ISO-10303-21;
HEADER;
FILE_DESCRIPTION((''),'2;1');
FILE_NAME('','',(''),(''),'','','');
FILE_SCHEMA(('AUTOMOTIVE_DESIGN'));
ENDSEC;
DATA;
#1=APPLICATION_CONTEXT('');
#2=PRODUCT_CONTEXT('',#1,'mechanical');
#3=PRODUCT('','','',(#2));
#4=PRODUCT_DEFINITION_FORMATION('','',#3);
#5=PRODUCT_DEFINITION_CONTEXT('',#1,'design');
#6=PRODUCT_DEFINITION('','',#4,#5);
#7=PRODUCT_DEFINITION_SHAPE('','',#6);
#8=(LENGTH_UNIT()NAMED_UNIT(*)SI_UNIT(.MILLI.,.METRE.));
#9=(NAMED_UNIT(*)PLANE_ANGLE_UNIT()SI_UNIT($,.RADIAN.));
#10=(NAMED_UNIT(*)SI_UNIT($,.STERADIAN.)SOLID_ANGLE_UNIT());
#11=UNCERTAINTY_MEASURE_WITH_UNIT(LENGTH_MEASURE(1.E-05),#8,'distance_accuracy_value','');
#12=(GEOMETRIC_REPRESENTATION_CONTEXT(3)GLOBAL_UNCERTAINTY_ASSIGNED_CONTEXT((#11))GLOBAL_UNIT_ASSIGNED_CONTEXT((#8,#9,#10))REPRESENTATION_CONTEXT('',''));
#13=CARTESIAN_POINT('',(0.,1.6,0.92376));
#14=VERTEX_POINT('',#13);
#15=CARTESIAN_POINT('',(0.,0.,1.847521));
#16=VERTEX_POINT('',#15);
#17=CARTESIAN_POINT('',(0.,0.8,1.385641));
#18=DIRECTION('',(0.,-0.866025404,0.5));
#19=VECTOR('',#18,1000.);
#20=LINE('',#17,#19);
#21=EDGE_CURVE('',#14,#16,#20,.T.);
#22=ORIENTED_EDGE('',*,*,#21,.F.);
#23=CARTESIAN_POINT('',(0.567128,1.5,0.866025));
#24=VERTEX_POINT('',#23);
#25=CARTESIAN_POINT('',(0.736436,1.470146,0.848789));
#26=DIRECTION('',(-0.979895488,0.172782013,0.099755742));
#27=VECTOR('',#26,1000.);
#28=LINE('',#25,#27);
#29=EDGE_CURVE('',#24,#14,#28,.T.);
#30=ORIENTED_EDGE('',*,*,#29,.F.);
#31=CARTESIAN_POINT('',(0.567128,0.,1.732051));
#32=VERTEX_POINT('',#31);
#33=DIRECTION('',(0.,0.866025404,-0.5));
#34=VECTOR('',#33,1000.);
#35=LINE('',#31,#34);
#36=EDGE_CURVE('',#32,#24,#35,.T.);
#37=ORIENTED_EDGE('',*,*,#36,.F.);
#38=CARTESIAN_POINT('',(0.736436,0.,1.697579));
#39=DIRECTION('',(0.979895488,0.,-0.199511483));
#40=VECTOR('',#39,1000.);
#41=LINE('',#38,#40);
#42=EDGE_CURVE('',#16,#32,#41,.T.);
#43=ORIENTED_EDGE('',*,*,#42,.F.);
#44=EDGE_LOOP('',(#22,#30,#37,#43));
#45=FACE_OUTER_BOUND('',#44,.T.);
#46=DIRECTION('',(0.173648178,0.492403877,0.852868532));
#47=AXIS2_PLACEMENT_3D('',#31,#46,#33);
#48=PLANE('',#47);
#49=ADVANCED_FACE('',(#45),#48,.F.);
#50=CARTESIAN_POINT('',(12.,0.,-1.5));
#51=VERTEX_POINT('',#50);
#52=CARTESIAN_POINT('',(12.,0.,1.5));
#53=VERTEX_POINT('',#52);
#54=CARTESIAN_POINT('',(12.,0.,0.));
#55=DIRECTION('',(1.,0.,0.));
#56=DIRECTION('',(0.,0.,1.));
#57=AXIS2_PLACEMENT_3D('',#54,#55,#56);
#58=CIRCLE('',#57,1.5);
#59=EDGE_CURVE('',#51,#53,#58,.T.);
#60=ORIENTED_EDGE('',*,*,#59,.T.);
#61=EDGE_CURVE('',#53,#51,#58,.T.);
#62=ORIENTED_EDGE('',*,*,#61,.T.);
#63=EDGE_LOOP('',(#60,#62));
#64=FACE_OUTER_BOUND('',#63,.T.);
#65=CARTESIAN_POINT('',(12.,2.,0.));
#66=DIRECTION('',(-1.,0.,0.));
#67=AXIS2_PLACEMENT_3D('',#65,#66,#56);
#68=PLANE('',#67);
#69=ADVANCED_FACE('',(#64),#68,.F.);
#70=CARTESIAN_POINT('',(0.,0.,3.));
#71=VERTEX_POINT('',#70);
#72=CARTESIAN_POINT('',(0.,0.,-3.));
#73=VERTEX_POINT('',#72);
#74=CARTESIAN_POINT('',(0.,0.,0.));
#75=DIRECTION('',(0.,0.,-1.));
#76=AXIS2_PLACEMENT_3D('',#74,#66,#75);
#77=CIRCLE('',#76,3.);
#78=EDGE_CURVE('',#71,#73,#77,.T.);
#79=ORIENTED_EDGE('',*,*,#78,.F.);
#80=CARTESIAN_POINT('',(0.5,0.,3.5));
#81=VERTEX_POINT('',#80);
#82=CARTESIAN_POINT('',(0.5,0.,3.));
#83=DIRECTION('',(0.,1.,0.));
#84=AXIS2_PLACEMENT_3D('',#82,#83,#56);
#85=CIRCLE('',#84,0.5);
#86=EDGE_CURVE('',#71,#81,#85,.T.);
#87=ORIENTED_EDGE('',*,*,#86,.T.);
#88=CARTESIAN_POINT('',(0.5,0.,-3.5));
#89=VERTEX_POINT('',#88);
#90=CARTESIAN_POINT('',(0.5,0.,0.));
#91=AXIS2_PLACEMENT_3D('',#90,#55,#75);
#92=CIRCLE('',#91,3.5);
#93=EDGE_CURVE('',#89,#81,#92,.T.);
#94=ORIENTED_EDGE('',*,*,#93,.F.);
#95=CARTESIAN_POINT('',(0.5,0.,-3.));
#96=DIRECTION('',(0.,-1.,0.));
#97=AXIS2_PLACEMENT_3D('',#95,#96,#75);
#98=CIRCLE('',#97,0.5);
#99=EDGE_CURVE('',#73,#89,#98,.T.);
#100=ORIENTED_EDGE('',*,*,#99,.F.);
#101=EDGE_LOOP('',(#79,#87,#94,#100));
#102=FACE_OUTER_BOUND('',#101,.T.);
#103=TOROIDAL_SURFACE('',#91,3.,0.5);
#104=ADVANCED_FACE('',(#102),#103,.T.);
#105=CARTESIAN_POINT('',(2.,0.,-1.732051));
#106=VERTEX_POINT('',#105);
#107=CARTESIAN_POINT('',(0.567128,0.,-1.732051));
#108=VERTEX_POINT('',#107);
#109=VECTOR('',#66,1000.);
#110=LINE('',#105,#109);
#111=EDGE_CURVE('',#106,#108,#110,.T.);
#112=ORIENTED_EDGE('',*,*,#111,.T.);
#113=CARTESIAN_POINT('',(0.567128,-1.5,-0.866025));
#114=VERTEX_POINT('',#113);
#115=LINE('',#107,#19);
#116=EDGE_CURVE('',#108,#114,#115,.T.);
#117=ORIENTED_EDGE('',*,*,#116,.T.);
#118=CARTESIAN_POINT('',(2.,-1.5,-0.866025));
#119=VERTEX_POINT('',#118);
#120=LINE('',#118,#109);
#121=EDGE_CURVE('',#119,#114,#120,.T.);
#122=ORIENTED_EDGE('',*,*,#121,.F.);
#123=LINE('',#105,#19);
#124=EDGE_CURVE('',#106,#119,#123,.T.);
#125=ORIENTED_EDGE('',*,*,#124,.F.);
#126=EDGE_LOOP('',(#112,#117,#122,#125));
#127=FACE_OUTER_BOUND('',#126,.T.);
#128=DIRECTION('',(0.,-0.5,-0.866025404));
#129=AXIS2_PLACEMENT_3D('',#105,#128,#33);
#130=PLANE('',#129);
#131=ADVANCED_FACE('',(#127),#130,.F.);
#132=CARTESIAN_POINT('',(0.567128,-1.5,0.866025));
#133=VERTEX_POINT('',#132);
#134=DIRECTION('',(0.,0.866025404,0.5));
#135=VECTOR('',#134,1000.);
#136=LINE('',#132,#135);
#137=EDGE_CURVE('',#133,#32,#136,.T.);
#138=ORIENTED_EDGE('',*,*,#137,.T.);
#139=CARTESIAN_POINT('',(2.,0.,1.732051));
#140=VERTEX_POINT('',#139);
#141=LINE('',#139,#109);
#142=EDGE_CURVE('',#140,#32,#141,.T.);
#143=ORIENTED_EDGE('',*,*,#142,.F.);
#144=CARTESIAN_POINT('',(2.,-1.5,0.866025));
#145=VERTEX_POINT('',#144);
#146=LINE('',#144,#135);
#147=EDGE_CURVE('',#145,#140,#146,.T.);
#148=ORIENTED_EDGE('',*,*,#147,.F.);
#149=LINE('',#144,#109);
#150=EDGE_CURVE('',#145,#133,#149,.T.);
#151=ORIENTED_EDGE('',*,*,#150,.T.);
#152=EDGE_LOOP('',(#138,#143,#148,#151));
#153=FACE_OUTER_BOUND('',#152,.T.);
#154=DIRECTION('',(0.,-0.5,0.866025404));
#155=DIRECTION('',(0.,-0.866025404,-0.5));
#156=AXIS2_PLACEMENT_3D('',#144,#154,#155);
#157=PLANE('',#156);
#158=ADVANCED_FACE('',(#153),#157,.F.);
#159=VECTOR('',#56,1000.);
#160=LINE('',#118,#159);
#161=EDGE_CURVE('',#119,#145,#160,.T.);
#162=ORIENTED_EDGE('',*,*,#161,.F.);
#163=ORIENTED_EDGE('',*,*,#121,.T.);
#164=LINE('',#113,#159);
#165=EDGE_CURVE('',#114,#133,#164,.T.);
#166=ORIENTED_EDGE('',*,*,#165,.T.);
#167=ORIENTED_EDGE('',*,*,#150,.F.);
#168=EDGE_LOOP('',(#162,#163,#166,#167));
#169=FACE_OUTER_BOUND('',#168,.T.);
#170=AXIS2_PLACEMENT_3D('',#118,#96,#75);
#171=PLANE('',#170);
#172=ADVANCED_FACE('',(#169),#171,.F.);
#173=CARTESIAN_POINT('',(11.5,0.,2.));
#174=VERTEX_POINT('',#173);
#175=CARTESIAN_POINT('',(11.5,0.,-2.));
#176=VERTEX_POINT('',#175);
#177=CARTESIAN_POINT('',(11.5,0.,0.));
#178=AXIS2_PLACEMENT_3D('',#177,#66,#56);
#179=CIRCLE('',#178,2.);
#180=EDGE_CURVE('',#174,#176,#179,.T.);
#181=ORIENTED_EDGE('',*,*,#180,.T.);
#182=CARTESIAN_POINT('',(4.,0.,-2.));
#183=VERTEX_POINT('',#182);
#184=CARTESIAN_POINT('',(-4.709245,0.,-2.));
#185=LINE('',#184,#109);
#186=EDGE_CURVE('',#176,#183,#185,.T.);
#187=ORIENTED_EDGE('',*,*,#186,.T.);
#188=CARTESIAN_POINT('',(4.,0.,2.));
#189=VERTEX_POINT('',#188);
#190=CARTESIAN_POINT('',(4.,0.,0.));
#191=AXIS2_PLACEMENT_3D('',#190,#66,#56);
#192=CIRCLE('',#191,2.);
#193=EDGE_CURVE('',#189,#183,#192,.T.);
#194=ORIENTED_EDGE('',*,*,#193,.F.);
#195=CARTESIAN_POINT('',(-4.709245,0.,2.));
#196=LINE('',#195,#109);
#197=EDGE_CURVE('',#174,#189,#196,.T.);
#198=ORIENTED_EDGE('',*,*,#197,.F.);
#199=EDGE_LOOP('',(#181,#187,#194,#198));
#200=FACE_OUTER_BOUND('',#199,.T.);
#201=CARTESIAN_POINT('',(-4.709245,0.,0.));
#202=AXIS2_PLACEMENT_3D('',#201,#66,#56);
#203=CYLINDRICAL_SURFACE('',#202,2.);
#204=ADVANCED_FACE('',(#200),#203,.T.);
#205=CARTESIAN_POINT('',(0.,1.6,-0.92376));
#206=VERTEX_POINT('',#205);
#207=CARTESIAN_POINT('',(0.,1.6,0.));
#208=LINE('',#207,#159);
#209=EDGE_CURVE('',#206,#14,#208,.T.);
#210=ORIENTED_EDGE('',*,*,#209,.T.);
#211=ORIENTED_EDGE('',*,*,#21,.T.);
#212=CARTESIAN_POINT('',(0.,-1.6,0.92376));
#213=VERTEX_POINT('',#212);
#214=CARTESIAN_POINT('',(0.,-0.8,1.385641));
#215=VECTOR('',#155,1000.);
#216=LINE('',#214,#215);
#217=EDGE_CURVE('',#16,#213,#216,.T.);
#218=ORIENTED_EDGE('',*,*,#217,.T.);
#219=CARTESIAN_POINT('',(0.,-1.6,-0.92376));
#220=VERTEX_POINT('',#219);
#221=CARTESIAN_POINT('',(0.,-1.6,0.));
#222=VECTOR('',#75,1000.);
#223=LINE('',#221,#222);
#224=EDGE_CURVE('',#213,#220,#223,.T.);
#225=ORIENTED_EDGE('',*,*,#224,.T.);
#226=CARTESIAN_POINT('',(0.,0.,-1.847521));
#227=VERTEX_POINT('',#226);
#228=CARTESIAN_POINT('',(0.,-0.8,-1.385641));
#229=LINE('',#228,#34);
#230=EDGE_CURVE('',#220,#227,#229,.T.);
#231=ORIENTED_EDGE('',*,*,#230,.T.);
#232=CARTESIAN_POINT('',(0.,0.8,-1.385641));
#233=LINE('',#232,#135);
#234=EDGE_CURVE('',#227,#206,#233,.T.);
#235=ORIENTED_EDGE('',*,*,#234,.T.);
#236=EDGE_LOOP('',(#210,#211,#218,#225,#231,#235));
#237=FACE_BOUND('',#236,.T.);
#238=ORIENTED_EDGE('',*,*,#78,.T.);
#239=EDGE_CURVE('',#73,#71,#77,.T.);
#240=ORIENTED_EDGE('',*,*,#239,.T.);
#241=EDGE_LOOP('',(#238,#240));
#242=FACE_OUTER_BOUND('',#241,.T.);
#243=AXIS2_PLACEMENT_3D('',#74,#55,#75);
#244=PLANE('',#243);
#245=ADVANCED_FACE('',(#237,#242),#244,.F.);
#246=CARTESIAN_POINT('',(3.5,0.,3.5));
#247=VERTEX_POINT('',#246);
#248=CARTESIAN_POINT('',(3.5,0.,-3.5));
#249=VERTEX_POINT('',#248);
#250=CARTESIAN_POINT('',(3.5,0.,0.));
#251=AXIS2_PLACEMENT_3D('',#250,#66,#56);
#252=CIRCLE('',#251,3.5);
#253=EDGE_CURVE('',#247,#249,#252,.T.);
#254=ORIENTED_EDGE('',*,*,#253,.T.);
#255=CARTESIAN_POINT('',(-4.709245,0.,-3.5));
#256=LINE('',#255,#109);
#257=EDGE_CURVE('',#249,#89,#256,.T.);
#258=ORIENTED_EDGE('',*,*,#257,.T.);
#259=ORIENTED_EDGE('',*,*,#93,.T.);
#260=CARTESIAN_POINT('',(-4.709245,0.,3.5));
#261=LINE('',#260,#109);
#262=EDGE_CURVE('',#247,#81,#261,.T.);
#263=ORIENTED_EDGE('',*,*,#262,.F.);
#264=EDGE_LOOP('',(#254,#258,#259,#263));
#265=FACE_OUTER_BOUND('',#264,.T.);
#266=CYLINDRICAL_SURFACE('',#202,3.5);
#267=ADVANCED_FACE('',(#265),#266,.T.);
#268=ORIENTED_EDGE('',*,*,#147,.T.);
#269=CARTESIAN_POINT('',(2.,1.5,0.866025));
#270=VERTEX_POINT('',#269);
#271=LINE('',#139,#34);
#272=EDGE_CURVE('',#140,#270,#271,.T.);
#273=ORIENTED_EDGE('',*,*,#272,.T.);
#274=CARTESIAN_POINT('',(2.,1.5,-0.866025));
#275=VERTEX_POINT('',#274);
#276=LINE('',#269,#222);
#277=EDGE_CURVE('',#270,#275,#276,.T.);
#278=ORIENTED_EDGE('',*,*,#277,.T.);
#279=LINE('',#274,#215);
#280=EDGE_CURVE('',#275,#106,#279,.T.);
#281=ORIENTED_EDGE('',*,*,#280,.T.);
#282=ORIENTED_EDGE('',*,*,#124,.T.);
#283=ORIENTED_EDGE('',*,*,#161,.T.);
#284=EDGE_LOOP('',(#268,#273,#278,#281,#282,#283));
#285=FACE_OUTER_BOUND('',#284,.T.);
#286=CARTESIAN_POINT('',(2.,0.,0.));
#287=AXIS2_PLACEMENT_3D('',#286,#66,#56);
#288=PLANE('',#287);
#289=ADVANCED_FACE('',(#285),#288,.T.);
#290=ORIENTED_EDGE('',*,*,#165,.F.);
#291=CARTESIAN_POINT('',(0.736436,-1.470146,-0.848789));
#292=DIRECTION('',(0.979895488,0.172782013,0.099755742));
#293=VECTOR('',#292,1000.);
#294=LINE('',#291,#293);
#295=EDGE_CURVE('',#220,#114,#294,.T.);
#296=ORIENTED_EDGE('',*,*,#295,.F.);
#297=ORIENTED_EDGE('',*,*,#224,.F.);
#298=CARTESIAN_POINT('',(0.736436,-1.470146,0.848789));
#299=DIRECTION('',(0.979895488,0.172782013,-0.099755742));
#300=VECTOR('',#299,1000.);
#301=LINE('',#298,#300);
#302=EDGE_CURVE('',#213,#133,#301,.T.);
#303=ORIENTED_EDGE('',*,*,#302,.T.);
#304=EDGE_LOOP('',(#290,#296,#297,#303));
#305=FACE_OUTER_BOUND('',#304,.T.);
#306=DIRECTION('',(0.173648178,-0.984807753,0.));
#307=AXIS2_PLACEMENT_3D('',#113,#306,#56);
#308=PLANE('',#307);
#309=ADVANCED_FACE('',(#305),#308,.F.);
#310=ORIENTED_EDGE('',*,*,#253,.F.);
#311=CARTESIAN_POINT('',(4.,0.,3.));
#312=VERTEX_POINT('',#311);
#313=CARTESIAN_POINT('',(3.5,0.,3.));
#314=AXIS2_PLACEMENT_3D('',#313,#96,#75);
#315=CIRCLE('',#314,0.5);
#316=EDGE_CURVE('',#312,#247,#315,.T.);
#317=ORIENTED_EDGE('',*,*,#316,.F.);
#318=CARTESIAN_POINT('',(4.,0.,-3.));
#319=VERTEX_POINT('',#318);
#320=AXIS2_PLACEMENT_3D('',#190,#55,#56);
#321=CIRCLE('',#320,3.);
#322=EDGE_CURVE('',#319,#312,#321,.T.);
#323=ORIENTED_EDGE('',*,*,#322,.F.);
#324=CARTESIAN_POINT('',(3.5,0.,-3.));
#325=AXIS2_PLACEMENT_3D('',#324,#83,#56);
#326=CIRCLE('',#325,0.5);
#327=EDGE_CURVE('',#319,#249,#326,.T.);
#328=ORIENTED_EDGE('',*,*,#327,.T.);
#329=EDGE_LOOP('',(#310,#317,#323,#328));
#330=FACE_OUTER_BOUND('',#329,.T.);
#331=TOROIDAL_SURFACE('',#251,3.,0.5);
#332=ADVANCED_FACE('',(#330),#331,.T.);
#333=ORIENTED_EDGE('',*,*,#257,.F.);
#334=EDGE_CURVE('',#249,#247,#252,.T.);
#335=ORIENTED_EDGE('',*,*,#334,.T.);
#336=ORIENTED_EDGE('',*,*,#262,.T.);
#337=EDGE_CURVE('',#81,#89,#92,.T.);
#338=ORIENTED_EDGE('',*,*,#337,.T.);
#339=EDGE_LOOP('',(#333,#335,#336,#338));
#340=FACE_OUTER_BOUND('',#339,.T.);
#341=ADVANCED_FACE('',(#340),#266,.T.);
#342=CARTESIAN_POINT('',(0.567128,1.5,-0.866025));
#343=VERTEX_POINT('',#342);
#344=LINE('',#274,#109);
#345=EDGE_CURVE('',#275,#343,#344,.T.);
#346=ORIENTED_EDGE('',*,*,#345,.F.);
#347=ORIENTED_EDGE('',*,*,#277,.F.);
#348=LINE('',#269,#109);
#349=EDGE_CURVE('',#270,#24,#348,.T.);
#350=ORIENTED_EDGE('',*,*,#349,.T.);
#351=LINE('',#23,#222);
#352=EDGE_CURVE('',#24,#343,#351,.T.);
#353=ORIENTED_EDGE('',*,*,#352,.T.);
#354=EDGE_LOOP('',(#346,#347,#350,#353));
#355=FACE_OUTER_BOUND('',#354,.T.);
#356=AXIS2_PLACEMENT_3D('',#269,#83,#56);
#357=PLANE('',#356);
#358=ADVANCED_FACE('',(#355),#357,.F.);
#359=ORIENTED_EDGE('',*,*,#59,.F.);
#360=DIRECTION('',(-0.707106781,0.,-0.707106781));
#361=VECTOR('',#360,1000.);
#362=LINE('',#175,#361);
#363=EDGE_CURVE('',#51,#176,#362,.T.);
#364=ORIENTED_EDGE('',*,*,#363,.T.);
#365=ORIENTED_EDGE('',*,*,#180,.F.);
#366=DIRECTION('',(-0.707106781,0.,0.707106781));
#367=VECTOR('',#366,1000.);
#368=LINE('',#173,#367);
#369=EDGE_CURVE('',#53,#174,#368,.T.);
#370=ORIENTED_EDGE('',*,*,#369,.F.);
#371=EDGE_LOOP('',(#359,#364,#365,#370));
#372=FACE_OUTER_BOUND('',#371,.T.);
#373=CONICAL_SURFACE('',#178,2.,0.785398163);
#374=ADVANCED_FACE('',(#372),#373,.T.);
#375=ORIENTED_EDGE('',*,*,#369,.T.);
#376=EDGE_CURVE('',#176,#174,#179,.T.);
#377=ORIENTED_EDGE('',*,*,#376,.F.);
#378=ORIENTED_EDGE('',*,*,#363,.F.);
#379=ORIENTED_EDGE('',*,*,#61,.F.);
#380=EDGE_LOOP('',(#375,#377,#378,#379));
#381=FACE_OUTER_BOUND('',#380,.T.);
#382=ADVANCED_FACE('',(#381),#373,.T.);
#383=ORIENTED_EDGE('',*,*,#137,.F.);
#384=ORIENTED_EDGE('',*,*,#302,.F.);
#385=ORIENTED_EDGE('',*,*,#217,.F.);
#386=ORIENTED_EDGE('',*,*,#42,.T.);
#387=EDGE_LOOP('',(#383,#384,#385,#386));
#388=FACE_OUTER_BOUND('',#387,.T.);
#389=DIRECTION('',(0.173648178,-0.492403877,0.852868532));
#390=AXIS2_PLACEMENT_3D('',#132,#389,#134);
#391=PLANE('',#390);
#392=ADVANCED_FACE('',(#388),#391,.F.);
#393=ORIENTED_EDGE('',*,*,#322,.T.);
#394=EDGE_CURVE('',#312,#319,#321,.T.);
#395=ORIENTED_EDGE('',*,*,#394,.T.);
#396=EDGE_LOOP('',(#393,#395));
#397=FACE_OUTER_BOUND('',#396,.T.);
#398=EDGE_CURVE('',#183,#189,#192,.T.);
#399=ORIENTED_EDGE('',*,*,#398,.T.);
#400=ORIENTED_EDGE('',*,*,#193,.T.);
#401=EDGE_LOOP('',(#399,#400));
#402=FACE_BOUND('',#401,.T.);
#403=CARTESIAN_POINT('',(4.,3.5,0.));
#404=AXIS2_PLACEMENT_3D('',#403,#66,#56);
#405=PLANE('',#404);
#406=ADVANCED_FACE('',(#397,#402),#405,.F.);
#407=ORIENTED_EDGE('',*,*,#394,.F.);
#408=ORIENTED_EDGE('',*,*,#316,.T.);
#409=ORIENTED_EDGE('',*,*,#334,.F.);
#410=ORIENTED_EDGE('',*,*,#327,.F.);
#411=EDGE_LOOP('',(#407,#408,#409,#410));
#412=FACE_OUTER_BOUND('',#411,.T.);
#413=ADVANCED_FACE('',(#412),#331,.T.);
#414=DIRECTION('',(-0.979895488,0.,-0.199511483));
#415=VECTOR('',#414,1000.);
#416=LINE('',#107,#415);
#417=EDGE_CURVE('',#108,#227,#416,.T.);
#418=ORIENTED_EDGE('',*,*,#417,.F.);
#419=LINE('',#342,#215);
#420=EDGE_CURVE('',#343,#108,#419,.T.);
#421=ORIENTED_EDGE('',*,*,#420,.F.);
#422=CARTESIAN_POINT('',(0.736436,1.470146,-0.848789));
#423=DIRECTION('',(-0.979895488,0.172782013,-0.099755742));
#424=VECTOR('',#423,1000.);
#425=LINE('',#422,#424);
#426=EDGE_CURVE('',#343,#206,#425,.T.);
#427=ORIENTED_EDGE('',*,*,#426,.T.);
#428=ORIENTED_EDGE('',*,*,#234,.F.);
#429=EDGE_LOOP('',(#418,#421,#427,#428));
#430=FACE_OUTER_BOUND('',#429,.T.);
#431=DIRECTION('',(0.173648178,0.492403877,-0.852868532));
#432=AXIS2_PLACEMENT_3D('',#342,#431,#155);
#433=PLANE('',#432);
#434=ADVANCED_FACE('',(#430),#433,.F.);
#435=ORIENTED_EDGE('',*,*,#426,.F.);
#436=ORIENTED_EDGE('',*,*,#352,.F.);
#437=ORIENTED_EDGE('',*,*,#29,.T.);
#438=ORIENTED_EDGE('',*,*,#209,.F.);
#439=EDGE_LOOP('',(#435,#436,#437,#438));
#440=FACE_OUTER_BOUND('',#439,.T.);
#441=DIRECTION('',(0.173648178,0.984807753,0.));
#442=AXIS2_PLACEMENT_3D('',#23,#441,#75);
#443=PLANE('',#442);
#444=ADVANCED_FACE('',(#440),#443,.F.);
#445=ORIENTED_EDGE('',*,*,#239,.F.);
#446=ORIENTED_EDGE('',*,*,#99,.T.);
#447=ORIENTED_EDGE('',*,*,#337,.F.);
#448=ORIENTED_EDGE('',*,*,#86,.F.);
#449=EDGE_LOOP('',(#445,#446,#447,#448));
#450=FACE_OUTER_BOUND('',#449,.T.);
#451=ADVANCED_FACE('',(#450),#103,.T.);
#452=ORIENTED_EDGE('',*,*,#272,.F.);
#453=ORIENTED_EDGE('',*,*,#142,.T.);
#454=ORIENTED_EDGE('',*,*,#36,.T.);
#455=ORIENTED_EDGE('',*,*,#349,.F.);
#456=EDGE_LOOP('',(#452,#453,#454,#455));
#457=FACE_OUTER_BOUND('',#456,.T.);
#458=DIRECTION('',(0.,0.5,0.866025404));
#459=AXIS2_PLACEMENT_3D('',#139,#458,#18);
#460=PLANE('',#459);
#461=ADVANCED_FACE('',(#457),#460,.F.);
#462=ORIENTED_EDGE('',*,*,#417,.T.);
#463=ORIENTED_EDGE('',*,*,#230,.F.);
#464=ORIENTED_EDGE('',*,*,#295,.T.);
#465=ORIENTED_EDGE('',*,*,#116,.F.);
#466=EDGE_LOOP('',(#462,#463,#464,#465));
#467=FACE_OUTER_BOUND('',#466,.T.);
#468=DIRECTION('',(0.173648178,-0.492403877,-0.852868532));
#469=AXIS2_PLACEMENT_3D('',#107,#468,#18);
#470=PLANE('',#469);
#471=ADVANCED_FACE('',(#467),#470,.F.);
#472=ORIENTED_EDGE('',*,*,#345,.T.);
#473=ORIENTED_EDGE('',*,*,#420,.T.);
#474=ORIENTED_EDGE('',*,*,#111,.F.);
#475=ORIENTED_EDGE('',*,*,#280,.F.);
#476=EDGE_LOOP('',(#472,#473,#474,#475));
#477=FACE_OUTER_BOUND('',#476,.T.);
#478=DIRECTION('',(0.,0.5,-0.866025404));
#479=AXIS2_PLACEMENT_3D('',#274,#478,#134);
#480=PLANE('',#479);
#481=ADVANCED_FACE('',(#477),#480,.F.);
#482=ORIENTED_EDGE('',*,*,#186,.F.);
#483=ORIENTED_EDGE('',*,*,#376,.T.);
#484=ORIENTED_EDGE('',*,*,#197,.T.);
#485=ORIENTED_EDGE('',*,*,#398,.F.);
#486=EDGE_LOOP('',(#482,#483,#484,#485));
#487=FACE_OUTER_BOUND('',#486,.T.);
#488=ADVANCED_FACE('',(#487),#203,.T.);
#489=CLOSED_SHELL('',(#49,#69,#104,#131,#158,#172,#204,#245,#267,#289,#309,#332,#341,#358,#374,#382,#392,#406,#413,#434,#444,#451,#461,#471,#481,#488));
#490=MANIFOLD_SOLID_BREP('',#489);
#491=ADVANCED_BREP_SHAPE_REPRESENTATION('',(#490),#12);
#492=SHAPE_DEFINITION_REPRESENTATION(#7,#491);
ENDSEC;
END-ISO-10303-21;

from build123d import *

# Parameters (mm, degrees)
CUT_EXTRUDE1_DEPTH = 2
FILLET1_R          = 0.5
CHAMFER1_SIZE      = 0.1
CHAMFER1_SIZE2     = 0.567128182
CHAMFER2_SIZE      = 0.5


with BuildPart() as part:
    # Sketch1 → Revolve1 (revolve)
    with BuildSketch(Plane.XY, mode=Mode.PRIVATE) as revolve1_sk:
        Polygon((0, 0), (0, 3.5), (4, 3.5), (4, 2), (12, 2), (12, 0), align=None)
    revolve(revolve1_sk.sketch.rotate(Axis((-4.709244637, 0, 0), (1, 0, 0)), 90), axis=Axis((-4.709244637, 0, 0), (1, 0, 0)))

    # Sketch4 → Cut-Extrude1 (cut)
    with BuildSketch(Plane.ZY):
        Polygon((-1.732050808, 0), (-0.866025404, -1.5), (0.866025404, -1.5), (1.732050808, 0), (0.866025404, 1.5), (-0.866025404, 1.5), align=None)
    extrude(amount=-CUT_EXTRUDE1_DEPTH, mode=Mode.SUBTRACT)

    # Fillet1
    fillet1_edges = [part.edges().sort_by_distance(p)[0] for p in [
        (4, 0, -3.5),
        (0, 0, -3.5),
    ]]
    fillet(fillet1_edges, radius=FILLET1_R)

    # Chamfer1
    chamfer1_edges = [part.edges().sort_by_distance(p)[0] for p in [
        (0, 0.75, -1.299038106),
        (0, -0.75, -1.299038106),
        (0, -1.5, 0),
        (0, -0.75, 1.299038106),
        (0, 0.75, 1.299038106),
        (0, 1.5, 0),
    ]]
    chamfer1_side = [part.faces().sort_by_distance(p)[0] for p in [
        (0, 0, -2.915147186),
    ]]
    chamfer(chamfer1_edges, length=CHAMFER1_SIZE, length2=CHAMFER1_SIZE2, reference=chamfer1_side[0])

    # Chamfer2
    chamfer2_edges = [part.edges().sort_by_distance(p)[0] for p in [
        (12, 0, -2),
    ]]
    chamfer(chamfer2_edges, length=CHAMFER2_SIZE)


solid = part.part
